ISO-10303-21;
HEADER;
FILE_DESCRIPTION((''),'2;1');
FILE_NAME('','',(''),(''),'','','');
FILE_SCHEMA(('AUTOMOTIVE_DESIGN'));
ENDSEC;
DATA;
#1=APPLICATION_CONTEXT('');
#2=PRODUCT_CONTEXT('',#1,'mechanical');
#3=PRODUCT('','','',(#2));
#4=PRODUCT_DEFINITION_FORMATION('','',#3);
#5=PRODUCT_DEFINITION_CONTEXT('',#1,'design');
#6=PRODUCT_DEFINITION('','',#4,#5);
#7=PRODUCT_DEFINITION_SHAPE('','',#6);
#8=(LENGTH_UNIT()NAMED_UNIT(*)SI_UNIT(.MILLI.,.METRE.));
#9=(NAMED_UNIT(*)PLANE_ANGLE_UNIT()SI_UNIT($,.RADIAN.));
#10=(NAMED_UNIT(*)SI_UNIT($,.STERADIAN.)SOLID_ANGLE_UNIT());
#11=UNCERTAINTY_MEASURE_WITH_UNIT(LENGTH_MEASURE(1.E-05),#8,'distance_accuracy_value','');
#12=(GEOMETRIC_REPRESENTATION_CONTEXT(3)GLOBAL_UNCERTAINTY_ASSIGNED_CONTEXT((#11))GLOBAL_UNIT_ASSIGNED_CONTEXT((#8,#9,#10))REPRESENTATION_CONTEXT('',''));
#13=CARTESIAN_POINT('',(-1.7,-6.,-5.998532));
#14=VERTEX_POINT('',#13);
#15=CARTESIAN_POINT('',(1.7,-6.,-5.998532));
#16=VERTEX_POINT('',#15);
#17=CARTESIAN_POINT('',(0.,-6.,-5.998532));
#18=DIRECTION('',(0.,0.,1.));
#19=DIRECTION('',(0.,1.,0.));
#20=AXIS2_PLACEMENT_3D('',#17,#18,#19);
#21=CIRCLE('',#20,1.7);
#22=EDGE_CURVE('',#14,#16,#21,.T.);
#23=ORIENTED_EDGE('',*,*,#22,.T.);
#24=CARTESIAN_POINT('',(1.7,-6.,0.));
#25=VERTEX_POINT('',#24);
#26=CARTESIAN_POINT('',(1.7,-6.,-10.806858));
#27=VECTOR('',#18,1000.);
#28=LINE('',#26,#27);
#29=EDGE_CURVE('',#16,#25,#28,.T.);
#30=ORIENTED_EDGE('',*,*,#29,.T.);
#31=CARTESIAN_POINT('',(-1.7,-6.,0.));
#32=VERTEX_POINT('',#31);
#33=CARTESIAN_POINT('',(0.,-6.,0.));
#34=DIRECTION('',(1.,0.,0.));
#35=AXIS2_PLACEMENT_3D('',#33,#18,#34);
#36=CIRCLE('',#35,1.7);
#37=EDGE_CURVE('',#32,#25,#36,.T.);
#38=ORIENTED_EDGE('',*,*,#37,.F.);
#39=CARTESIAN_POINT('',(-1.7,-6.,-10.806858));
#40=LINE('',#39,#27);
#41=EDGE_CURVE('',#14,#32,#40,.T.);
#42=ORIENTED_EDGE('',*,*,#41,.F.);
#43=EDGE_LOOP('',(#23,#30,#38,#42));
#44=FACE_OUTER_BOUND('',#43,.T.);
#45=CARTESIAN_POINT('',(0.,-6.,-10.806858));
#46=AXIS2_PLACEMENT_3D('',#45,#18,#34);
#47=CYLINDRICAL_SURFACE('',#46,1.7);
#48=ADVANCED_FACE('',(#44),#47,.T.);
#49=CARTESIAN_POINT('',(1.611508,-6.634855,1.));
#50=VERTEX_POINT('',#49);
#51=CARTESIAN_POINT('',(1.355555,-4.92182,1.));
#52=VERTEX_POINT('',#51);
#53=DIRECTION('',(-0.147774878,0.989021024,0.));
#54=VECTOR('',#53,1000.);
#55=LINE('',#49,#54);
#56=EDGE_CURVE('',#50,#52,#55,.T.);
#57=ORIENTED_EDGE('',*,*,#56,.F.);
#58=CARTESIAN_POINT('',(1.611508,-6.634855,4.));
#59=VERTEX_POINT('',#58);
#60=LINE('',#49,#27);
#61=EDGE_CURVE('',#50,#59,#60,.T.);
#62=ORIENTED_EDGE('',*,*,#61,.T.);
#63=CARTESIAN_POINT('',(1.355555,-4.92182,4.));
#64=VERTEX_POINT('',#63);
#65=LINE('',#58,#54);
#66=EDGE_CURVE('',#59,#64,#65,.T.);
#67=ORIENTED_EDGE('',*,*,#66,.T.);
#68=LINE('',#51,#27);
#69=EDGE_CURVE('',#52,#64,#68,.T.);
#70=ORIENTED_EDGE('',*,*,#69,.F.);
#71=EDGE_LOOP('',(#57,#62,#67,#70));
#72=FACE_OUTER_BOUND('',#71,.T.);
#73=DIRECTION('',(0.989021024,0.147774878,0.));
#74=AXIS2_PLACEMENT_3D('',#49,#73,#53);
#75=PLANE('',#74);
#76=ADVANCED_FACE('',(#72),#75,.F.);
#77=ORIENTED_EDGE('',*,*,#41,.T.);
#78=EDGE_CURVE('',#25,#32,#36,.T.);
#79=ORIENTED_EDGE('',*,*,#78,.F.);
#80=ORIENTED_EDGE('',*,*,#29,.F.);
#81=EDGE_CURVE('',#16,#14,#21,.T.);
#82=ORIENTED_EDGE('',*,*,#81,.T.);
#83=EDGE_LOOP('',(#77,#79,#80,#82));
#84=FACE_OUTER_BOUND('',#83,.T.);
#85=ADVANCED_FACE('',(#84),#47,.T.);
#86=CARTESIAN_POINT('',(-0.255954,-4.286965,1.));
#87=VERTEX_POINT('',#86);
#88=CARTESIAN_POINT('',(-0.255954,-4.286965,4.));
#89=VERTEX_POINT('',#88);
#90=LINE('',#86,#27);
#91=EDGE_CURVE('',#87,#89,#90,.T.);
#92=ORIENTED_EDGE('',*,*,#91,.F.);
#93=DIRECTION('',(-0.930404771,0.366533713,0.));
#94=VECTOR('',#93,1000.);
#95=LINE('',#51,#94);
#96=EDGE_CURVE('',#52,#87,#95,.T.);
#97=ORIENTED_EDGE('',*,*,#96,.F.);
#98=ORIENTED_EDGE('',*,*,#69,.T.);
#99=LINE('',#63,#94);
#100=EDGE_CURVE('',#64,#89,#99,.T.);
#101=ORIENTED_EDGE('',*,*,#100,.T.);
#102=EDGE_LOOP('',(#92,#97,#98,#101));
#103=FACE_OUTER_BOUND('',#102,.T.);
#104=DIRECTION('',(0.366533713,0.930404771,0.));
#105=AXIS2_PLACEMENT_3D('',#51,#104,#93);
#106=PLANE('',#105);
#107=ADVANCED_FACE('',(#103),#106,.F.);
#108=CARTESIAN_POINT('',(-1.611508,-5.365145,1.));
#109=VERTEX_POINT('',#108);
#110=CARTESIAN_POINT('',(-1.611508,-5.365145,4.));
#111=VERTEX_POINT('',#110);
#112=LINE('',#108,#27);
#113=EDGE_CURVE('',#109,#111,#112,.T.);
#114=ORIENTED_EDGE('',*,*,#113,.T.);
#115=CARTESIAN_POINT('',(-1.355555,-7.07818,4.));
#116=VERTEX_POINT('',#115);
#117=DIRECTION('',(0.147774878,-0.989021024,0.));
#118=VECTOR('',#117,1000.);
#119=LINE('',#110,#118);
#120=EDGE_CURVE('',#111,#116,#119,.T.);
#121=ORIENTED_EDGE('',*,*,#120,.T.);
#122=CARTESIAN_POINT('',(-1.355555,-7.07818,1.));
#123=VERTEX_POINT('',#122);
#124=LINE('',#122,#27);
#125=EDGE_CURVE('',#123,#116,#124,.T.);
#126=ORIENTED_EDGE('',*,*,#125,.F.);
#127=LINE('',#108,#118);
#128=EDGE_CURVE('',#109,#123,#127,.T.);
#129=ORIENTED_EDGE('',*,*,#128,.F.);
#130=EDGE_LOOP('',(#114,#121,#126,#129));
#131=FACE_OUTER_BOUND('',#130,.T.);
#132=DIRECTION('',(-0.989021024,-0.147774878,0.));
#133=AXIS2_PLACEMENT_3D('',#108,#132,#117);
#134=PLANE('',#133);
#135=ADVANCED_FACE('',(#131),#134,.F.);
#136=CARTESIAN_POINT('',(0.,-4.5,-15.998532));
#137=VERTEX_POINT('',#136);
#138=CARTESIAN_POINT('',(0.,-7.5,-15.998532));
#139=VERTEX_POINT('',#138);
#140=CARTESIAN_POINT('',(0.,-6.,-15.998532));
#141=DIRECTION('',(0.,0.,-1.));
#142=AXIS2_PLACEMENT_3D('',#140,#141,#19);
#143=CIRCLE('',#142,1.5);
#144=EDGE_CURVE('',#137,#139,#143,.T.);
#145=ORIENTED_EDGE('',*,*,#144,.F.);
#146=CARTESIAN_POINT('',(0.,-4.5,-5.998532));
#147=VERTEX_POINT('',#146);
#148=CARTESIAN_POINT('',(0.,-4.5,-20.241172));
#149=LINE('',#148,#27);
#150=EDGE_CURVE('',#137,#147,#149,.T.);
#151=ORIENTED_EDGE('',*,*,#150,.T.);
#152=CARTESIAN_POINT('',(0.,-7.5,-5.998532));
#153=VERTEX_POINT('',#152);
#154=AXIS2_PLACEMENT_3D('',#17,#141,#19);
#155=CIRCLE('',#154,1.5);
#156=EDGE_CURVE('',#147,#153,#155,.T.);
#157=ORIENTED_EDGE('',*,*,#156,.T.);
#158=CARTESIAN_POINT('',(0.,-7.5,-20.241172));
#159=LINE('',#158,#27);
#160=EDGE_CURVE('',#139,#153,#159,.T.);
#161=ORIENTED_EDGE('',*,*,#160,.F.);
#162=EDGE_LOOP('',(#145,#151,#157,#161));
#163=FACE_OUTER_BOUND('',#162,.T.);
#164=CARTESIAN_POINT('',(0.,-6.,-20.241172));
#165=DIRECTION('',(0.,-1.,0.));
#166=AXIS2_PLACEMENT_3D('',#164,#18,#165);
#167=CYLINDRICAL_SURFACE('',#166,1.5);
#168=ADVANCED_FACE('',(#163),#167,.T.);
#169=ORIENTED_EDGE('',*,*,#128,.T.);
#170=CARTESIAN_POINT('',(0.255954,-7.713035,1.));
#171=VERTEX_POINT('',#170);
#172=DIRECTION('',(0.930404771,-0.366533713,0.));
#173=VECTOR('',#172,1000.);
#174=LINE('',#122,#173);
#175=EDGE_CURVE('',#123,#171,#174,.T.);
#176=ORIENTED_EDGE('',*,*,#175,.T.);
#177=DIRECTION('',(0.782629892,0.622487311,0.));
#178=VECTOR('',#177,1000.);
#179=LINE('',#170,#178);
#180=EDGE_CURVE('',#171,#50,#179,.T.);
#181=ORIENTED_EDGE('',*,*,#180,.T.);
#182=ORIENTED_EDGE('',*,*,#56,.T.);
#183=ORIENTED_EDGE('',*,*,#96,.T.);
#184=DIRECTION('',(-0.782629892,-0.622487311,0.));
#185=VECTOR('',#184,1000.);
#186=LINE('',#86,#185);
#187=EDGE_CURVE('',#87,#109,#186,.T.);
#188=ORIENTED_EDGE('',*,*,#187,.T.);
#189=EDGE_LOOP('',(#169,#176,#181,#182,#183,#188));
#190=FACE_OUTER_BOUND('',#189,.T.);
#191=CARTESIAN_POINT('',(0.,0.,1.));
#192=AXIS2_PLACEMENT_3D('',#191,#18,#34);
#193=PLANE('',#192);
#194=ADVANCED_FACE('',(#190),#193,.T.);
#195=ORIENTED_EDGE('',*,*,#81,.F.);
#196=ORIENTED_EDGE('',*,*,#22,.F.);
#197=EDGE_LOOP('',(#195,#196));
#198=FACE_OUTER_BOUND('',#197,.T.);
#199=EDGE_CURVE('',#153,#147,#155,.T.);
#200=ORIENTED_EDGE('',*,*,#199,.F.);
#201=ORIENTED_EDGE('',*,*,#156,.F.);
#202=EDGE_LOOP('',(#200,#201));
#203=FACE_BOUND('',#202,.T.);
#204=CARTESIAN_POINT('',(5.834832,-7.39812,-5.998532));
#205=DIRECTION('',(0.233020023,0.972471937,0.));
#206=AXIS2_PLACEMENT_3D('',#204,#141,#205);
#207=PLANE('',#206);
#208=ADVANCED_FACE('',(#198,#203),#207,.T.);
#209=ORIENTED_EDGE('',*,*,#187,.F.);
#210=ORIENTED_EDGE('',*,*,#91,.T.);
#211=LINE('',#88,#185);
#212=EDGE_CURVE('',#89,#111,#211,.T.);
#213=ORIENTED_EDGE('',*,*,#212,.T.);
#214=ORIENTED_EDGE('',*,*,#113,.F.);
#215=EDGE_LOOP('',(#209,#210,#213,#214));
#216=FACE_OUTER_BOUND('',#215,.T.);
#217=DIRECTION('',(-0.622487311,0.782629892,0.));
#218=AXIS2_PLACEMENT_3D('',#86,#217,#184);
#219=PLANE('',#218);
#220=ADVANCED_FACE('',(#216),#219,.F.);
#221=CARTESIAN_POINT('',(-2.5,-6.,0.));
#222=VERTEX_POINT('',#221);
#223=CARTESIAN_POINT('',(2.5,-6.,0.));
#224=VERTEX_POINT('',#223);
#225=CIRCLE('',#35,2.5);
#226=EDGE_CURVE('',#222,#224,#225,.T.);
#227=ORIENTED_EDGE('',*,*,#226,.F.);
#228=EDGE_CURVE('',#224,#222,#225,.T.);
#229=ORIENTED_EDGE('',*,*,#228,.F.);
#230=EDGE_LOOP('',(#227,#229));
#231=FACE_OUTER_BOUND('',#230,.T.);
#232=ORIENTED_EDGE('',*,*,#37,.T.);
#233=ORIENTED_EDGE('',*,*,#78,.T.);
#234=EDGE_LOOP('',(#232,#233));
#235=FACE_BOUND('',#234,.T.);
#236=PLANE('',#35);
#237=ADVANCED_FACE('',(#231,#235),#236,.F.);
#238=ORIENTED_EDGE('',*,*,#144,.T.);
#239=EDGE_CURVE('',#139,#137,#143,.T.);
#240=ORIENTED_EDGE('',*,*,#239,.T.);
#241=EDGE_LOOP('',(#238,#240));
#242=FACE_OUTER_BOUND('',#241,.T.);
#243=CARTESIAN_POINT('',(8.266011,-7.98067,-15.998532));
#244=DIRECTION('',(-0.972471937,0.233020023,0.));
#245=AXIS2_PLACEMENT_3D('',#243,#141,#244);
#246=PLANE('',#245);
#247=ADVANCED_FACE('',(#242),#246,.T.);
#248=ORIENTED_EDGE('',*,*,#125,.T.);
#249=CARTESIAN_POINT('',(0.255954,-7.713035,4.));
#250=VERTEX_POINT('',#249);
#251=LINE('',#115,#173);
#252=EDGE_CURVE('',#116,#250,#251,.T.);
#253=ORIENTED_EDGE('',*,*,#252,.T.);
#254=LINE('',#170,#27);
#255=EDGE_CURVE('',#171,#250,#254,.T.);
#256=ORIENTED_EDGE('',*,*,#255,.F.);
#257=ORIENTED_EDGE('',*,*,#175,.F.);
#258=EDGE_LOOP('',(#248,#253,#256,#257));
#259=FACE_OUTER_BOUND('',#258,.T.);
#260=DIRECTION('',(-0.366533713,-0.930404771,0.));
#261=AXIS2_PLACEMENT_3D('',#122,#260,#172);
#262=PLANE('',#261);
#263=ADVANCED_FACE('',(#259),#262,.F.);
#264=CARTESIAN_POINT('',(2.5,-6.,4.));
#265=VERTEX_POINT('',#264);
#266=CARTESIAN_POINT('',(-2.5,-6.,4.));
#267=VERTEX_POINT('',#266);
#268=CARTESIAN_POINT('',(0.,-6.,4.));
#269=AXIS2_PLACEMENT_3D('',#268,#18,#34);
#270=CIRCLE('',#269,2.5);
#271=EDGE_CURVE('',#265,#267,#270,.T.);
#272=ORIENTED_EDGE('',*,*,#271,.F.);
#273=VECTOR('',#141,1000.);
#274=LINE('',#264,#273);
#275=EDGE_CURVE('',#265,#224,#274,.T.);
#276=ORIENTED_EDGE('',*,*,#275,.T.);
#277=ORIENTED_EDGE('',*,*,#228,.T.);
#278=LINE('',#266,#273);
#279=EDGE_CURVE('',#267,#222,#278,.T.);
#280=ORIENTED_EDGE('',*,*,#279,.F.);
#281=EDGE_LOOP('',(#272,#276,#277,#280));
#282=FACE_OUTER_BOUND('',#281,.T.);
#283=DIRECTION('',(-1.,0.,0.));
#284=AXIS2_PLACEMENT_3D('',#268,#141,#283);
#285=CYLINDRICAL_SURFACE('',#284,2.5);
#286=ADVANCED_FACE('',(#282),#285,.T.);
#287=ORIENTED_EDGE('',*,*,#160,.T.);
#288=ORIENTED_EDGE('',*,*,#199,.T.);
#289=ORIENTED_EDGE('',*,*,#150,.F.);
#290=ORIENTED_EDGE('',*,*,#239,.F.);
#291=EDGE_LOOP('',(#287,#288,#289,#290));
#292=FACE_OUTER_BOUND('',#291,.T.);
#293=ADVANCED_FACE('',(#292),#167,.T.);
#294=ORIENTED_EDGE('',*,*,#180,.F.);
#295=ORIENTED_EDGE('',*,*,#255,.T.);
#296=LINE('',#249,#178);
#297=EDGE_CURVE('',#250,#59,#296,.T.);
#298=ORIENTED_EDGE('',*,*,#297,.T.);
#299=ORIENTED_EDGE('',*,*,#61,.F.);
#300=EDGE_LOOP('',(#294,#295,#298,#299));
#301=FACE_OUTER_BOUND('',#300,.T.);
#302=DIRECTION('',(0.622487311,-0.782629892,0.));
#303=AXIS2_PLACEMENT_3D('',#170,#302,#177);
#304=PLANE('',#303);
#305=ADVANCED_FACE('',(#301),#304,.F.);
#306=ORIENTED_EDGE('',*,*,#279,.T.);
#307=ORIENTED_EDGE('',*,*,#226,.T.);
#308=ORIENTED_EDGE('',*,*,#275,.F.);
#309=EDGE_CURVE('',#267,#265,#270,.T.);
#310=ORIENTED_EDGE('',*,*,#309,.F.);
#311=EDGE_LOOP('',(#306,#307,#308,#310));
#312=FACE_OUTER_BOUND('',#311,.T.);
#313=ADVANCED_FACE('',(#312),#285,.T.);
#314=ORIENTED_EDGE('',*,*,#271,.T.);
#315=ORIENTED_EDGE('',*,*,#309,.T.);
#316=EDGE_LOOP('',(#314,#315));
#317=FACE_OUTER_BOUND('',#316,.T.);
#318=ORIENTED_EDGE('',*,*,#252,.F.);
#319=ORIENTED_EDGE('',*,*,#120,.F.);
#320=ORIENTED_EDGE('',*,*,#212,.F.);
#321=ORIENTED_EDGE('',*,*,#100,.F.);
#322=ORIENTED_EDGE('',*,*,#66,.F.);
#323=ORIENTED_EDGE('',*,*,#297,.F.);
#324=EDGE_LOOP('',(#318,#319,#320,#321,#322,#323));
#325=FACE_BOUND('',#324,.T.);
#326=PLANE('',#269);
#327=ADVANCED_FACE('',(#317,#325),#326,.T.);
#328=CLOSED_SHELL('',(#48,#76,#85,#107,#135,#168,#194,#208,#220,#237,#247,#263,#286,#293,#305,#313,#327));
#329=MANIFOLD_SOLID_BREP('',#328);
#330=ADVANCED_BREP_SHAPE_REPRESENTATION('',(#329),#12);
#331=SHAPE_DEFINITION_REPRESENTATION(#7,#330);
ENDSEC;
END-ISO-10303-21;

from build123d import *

# Parameters (mm, degrees)
SKETCH_1_R          = 1.7
EXTRUDE_1_DEPTH     = 5.998531593
SKETCH_2_R          = 1.5
EXTRUDE_2_DEPTH     = 10
SKETCH_3_R          = 2.5
EXTRUDE_3_DEPTH     = 4
CUT_EXTRUDE_1_DEPTH = 3


with BuildPart() as part:
    # 草图1 → 凸台-拉伸1 (new body)
    with BuildSketch(Plane.XY):
        with Locations((0, -6)):
            Circle(SKETCH_1_R)
    extrude(amount=-EXTRUDE_1_DEPTH)

    # 草图2 → 凸台-拉伸2 (add)
    with BuildSketch(Plane(origin=(0, 0, -5.998531593), x_dir=(-1, 0, 0), z_dir=(0, 0, -1))):
        with Locations(Location((0, -6, 0), (0, 0, 90))):
            Circle(SKETCH_2_R)
    extrude(amount=EXTRUDE_2_DEPTH)

    # 草图3 → 凸台-拉伸3 (add)
    with BuildSketch(Plane.XY):
        with Locations((0, -6)):
            Circle(SKETCH_3_R)
    extrude(amount=EXTRUDE_3_DEPTH)

    # 草图4 → 切除-拉伸1 (cut)
    with BuildSketch(Plane.XY.offset(4)):
        Polygon((1.355554736, -4.921820351), (-0.255953598, -4.286965337), (-1.611508335, -5.365144986), (-1.355554737, -7.078179649), (0.255953597, -7.713034663), (1.611508334, -6.634855014), align=None)
    extrude(amount=-CUT_EXTRUDE_1_DEPTH, mode=Mode.SUBTRACT)


solid = part.part
